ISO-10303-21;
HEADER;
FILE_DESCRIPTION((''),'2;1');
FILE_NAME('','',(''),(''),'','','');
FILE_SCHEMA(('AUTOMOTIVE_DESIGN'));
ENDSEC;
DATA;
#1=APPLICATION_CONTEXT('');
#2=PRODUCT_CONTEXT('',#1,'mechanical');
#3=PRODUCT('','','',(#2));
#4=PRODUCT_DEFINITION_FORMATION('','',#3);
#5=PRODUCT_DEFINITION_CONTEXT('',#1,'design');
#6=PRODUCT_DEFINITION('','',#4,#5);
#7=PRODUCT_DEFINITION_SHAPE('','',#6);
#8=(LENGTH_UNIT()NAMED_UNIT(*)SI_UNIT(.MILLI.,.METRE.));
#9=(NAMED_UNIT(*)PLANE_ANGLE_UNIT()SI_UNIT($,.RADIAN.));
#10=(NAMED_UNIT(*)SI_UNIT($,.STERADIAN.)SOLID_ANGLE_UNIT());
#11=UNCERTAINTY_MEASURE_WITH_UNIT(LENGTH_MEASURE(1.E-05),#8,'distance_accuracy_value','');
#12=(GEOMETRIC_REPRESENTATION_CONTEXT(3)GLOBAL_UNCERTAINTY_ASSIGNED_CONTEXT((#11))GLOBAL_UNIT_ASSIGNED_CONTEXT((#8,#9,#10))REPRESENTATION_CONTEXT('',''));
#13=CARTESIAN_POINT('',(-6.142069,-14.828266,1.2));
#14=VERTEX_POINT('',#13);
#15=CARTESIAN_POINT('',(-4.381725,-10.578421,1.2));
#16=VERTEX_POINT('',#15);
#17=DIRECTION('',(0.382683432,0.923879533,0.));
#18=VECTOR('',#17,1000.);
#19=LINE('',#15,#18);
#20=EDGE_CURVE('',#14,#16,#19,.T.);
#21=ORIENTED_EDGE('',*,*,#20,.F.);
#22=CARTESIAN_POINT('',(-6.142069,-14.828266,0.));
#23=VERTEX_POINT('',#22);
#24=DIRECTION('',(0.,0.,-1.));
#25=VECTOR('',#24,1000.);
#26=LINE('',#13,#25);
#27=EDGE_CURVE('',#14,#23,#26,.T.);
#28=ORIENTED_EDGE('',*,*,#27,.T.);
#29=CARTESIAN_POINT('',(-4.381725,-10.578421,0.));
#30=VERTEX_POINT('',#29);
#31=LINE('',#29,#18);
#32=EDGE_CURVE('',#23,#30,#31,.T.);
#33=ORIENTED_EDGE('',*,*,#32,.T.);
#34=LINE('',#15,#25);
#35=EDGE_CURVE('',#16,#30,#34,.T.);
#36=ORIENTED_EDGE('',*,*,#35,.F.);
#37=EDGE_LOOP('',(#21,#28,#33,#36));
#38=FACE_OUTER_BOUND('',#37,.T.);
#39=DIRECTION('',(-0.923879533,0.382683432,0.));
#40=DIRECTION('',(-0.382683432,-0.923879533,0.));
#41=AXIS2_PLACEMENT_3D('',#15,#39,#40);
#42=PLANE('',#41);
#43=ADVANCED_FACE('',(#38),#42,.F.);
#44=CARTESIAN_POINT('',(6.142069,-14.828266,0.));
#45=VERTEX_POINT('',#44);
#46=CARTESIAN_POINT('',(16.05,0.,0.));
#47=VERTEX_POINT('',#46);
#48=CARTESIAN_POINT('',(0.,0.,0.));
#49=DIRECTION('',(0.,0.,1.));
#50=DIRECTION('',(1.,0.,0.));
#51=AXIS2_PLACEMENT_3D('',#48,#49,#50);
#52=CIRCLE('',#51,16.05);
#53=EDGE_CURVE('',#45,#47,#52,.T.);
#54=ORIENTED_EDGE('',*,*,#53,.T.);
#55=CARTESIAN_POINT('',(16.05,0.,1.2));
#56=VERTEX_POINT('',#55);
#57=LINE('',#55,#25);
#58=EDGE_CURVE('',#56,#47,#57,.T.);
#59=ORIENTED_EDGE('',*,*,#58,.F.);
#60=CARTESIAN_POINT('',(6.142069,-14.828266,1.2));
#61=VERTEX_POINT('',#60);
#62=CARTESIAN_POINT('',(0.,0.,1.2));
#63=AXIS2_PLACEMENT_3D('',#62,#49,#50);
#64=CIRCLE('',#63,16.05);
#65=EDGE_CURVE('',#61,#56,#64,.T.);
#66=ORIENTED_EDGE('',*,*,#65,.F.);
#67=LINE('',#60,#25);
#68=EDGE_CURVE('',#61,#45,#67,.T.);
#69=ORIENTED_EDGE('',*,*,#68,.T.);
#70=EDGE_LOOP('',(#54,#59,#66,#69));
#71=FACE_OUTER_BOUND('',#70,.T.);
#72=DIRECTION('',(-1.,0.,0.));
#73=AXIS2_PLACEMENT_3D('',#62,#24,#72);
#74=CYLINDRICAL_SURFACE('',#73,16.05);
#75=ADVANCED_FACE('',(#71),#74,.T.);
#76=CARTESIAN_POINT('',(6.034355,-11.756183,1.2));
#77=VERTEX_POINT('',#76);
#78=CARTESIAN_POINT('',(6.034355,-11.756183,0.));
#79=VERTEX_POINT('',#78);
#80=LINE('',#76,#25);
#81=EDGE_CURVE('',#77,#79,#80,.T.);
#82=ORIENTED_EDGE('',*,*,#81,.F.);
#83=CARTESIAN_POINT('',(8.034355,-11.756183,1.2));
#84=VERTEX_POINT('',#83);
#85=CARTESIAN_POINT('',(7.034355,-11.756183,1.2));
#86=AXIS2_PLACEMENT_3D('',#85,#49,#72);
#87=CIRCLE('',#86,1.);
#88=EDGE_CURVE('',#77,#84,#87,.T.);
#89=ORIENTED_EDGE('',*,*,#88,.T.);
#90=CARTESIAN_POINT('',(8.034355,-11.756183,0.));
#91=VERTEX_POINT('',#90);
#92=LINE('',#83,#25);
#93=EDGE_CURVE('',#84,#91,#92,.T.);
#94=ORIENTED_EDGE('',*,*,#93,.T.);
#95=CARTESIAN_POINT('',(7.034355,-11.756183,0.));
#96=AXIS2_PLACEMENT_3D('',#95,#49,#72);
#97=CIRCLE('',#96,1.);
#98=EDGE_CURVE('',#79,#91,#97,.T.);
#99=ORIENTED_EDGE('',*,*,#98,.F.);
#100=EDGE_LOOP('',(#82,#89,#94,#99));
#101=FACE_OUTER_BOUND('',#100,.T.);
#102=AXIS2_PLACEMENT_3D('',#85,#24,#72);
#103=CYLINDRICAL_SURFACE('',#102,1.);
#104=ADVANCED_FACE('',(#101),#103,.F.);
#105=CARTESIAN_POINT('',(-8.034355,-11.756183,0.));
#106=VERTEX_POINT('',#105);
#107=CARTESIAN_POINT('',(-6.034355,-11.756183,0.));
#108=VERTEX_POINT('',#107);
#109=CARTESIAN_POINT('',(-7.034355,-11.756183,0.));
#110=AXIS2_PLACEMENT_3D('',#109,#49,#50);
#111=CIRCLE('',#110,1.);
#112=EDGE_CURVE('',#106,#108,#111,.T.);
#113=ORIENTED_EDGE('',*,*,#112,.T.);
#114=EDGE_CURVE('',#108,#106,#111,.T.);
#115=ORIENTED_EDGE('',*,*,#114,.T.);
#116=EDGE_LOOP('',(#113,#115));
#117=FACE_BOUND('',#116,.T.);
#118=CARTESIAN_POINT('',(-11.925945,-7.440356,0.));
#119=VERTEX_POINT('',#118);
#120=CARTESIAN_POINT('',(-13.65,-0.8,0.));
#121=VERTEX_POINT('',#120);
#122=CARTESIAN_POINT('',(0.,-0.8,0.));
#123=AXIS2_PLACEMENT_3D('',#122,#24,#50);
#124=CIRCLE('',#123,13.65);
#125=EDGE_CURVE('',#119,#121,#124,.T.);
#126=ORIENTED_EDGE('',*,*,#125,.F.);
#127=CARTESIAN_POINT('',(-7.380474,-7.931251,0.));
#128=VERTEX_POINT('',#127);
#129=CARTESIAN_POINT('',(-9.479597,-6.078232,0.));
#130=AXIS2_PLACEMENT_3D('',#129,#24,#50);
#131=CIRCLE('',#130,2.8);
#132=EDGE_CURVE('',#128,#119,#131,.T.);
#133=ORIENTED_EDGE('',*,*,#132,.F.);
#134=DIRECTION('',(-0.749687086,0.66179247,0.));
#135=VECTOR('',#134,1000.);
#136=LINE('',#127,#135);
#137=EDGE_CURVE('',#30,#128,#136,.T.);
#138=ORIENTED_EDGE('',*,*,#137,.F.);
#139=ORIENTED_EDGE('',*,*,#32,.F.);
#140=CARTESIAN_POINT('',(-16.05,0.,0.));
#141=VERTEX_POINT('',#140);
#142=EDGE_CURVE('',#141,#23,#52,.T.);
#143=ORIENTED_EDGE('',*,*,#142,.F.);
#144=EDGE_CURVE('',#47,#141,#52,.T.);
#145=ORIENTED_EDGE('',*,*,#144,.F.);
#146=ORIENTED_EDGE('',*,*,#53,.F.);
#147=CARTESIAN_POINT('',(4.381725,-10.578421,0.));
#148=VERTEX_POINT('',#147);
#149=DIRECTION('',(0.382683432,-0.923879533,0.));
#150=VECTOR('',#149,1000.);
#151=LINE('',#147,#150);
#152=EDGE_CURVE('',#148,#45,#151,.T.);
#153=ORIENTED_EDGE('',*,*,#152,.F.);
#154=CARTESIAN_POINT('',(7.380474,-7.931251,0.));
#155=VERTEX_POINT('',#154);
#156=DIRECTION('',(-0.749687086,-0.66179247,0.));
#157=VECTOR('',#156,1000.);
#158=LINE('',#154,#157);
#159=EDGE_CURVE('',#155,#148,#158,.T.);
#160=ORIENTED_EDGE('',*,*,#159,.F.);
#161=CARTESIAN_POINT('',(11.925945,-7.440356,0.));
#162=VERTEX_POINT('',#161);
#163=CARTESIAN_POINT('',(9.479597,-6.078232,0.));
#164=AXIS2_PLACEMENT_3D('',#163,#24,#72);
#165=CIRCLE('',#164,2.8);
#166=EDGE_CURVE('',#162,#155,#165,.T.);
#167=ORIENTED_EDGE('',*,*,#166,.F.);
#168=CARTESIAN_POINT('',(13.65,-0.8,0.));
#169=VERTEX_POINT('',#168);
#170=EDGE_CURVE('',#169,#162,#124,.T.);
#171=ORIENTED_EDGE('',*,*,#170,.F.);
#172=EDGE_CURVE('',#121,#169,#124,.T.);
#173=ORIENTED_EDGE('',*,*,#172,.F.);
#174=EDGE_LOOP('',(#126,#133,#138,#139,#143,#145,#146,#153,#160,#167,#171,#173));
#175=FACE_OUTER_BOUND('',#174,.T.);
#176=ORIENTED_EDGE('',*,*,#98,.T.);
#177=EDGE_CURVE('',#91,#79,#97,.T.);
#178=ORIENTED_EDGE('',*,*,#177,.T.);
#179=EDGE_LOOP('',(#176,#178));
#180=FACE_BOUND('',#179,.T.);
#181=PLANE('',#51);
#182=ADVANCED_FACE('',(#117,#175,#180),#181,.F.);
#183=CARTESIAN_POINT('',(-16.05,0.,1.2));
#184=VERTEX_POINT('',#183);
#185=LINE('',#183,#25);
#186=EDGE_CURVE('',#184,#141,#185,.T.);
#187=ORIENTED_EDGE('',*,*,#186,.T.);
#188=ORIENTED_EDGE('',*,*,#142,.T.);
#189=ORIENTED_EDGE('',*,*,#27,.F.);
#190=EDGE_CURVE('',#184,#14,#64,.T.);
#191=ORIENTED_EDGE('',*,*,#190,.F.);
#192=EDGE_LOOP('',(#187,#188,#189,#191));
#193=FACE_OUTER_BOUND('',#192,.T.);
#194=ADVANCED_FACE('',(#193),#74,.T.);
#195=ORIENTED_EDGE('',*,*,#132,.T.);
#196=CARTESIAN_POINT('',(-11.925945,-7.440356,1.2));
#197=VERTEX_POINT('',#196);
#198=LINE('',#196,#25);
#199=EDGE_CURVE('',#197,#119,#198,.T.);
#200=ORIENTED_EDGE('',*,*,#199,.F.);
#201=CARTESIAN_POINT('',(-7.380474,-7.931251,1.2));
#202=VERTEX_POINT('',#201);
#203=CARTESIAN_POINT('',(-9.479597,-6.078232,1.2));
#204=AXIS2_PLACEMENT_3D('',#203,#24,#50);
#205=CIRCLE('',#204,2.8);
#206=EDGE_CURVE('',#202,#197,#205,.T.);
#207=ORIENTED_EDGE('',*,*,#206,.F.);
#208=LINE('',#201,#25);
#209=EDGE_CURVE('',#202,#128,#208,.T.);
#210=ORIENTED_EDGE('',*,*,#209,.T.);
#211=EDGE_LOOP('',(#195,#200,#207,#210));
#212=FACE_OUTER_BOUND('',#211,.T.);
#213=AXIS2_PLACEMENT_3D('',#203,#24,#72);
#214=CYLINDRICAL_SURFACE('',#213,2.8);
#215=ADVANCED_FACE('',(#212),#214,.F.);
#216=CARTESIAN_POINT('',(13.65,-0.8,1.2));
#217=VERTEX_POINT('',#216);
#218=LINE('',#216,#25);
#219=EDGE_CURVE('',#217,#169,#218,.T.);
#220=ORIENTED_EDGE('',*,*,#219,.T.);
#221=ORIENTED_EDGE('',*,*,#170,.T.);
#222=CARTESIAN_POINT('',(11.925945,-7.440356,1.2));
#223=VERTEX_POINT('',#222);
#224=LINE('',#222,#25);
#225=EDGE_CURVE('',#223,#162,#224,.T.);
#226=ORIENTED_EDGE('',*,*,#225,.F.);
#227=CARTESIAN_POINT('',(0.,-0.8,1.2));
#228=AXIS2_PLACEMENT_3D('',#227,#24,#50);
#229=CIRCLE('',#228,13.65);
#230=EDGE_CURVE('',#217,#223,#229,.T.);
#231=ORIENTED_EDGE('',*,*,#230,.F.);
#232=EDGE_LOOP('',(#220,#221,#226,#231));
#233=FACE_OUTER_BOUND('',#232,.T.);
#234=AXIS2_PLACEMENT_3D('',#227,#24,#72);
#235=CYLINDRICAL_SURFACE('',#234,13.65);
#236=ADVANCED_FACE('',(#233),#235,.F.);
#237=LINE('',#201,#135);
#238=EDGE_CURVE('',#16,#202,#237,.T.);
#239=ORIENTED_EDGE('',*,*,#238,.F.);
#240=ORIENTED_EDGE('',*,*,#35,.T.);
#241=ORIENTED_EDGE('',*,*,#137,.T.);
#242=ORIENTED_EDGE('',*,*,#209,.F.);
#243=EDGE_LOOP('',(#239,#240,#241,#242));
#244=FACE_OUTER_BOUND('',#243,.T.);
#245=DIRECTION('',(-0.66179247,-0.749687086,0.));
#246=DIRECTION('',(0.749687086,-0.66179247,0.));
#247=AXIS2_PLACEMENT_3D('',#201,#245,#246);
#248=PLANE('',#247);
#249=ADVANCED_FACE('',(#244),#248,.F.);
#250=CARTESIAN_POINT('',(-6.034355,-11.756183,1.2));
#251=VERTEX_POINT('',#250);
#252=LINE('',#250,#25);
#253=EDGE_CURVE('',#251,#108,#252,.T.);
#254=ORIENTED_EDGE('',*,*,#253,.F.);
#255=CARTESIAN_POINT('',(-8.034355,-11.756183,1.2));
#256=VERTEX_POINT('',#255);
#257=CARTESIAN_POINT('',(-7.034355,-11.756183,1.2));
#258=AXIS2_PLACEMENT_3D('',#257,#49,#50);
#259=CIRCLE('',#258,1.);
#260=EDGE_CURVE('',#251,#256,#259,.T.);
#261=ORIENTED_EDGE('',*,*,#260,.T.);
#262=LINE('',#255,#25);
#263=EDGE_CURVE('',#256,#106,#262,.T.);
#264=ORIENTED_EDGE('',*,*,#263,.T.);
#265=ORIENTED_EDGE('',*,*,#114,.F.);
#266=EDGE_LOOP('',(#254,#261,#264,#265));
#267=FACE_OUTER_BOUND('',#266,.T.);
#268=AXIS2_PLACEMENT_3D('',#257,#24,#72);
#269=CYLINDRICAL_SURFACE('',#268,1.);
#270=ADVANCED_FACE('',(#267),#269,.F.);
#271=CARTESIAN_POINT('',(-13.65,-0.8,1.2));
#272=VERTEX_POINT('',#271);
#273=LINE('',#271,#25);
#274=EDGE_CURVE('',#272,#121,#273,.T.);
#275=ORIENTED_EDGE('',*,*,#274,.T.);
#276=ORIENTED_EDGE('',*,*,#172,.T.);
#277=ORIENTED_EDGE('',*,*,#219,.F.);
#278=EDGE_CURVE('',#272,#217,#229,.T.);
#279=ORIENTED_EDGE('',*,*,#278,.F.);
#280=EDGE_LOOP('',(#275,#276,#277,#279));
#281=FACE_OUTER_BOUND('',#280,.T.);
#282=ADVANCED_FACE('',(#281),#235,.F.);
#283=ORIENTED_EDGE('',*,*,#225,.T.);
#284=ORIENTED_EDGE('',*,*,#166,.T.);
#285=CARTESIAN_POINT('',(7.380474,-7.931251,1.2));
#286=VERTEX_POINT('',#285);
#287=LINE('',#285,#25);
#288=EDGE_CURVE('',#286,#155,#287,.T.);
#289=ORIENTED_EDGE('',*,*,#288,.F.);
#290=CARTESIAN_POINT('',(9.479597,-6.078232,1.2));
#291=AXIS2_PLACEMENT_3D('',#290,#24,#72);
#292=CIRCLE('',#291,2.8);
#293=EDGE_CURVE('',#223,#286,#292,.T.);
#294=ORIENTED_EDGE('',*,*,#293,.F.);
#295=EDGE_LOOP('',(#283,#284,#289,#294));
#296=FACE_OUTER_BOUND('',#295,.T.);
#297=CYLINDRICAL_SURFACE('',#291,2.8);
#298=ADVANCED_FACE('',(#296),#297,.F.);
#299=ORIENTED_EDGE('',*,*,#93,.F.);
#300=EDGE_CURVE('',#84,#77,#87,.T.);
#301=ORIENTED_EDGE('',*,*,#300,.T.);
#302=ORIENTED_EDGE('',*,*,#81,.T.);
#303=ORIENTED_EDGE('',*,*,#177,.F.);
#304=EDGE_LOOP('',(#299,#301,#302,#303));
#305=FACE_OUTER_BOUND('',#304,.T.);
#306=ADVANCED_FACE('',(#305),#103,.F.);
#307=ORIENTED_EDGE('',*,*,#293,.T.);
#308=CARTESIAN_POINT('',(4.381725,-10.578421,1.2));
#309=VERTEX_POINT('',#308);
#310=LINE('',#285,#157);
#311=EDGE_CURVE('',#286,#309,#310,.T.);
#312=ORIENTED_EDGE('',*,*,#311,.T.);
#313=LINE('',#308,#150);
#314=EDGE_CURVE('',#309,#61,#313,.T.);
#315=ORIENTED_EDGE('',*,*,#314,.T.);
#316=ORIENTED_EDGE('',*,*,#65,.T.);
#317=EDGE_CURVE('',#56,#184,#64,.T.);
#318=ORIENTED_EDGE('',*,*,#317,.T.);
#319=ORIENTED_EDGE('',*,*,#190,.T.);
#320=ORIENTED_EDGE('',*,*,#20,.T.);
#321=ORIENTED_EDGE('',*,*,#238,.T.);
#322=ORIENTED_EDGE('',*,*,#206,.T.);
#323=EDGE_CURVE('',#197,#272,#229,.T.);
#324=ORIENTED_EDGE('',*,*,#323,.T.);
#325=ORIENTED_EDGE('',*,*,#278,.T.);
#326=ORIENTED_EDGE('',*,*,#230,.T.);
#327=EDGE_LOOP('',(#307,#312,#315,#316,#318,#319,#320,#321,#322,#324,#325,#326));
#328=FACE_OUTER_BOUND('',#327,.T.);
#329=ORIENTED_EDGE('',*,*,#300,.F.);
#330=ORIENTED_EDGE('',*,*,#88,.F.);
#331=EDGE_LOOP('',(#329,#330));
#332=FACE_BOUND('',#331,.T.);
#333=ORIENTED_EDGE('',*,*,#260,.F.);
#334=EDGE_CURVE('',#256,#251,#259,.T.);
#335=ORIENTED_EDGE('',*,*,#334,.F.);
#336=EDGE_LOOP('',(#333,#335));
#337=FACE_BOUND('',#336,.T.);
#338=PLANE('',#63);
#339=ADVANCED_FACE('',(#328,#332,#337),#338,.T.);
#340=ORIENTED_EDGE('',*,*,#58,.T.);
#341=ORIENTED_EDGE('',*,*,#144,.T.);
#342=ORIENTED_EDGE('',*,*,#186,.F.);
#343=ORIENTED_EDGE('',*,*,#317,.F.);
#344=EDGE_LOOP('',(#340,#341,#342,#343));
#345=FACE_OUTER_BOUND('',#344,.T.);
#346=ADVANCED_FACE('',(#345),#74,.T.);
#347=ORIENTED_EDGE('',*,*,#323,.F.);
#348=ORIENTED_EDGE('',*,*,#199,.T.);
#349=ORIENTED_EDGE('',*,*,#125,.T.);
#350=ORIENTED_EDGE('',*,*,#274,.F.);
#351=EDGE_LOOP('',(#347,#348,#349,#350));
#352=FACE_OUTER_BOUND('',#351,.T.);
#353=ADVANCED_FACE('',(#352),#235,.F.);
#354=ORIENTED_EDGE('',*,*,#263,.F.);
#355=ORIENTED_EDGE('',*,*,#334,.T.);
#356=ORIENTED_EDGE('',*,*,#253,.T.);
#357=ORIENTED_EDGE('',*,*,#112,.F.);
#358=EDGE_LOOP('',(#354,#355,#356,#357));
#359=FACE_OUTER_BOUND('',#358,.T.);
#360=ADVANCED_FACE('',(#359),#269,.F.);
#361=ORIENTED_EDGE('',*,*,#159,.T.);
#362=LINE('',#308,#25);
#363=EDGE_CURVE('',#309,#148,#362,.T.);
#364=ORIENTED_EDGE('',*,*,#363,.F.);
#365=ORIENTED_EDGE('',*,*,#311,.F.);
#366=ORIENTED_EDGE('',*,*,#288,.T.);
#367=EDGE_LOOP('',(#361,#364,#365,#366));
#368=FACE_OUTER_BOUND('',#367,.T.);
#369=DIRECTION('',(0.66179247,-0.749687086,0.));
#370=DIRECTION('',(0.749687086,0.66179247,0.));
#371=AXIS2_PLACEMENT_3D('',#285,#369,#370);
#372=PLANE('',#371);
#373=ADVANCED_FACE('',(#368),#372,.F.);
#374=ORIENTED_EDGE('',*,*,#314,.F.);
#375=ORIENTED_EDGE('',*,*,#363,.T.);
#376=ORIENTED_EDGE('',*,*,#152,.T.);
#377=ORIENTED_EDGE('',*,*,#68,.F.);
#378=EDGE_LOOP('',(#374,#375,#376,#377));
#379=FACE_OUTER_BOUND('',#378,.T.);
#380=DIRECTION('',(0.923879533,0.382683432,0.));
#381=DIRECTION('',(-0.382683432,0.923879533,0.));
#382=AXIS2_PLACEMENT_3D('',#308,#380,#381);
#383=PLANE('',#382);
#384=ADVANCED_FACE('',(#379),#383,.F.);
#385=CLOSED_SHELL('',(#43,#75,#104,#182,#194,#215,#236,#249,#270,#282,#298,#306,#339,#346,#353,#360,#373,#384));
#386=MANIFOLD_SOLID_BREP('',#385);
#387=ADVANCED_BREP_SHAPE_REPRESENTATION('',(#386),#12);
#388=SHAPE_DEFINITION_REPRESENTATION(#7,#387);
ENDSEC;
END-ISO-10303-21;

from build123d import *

# Parameters (mm, degrees)
SKETCH_1_R        = 1
EXTRUDE_952_DEPTH = 1.2


with BuildPart() as part:
    # 草图1 → Extrude 952 (new body)
    with BuildSketch(Plane.XY):
        with BuildLine():
            Line((-7.380473645, -7.931250769), (-4.381725301, -10.578420647))
            Line((-4.381725301, -10.578420647), (-6.142069089, -14.828266497))
            ThreePointArc((-6.142069089, -14.828266497), (0, 16.05), (6.142069089, -14.828266497))
            Line((6.142069089, -14.828266497), (4.381725301, -10.578420647))
            Line((4.381725301, -10.578420647), (7.380473645, -7.931250769))
            ThreePointArc((7.380473645, -7.931250769), (9.780239262, -8.8620448), (11.925945225, -7.440356203))
            ThreePointArc((11.925945225, -7.440356203), (0, 12.85), (-11.925945225, -7.440356203))
            ThreePointArc((-11.925945225, -7.440356203), (-9.780239262, -8.8620448), (-7.380473645, -7.931250769))
        make_face()
        with Locations((-7.034355028, -11.756183451)):
            Circle(SKETCH_1_R, mode=Mode.SUBTRACT)
        with Locations(Location((7.034355028, -11.756183451, 0), (0, 0, 180))):
            Circle(SKETCH_1_R, mode=Mode.SUBTRACT)
    extrude(amount=EXTRUDE_952_DEPTH)


solid = part.part
